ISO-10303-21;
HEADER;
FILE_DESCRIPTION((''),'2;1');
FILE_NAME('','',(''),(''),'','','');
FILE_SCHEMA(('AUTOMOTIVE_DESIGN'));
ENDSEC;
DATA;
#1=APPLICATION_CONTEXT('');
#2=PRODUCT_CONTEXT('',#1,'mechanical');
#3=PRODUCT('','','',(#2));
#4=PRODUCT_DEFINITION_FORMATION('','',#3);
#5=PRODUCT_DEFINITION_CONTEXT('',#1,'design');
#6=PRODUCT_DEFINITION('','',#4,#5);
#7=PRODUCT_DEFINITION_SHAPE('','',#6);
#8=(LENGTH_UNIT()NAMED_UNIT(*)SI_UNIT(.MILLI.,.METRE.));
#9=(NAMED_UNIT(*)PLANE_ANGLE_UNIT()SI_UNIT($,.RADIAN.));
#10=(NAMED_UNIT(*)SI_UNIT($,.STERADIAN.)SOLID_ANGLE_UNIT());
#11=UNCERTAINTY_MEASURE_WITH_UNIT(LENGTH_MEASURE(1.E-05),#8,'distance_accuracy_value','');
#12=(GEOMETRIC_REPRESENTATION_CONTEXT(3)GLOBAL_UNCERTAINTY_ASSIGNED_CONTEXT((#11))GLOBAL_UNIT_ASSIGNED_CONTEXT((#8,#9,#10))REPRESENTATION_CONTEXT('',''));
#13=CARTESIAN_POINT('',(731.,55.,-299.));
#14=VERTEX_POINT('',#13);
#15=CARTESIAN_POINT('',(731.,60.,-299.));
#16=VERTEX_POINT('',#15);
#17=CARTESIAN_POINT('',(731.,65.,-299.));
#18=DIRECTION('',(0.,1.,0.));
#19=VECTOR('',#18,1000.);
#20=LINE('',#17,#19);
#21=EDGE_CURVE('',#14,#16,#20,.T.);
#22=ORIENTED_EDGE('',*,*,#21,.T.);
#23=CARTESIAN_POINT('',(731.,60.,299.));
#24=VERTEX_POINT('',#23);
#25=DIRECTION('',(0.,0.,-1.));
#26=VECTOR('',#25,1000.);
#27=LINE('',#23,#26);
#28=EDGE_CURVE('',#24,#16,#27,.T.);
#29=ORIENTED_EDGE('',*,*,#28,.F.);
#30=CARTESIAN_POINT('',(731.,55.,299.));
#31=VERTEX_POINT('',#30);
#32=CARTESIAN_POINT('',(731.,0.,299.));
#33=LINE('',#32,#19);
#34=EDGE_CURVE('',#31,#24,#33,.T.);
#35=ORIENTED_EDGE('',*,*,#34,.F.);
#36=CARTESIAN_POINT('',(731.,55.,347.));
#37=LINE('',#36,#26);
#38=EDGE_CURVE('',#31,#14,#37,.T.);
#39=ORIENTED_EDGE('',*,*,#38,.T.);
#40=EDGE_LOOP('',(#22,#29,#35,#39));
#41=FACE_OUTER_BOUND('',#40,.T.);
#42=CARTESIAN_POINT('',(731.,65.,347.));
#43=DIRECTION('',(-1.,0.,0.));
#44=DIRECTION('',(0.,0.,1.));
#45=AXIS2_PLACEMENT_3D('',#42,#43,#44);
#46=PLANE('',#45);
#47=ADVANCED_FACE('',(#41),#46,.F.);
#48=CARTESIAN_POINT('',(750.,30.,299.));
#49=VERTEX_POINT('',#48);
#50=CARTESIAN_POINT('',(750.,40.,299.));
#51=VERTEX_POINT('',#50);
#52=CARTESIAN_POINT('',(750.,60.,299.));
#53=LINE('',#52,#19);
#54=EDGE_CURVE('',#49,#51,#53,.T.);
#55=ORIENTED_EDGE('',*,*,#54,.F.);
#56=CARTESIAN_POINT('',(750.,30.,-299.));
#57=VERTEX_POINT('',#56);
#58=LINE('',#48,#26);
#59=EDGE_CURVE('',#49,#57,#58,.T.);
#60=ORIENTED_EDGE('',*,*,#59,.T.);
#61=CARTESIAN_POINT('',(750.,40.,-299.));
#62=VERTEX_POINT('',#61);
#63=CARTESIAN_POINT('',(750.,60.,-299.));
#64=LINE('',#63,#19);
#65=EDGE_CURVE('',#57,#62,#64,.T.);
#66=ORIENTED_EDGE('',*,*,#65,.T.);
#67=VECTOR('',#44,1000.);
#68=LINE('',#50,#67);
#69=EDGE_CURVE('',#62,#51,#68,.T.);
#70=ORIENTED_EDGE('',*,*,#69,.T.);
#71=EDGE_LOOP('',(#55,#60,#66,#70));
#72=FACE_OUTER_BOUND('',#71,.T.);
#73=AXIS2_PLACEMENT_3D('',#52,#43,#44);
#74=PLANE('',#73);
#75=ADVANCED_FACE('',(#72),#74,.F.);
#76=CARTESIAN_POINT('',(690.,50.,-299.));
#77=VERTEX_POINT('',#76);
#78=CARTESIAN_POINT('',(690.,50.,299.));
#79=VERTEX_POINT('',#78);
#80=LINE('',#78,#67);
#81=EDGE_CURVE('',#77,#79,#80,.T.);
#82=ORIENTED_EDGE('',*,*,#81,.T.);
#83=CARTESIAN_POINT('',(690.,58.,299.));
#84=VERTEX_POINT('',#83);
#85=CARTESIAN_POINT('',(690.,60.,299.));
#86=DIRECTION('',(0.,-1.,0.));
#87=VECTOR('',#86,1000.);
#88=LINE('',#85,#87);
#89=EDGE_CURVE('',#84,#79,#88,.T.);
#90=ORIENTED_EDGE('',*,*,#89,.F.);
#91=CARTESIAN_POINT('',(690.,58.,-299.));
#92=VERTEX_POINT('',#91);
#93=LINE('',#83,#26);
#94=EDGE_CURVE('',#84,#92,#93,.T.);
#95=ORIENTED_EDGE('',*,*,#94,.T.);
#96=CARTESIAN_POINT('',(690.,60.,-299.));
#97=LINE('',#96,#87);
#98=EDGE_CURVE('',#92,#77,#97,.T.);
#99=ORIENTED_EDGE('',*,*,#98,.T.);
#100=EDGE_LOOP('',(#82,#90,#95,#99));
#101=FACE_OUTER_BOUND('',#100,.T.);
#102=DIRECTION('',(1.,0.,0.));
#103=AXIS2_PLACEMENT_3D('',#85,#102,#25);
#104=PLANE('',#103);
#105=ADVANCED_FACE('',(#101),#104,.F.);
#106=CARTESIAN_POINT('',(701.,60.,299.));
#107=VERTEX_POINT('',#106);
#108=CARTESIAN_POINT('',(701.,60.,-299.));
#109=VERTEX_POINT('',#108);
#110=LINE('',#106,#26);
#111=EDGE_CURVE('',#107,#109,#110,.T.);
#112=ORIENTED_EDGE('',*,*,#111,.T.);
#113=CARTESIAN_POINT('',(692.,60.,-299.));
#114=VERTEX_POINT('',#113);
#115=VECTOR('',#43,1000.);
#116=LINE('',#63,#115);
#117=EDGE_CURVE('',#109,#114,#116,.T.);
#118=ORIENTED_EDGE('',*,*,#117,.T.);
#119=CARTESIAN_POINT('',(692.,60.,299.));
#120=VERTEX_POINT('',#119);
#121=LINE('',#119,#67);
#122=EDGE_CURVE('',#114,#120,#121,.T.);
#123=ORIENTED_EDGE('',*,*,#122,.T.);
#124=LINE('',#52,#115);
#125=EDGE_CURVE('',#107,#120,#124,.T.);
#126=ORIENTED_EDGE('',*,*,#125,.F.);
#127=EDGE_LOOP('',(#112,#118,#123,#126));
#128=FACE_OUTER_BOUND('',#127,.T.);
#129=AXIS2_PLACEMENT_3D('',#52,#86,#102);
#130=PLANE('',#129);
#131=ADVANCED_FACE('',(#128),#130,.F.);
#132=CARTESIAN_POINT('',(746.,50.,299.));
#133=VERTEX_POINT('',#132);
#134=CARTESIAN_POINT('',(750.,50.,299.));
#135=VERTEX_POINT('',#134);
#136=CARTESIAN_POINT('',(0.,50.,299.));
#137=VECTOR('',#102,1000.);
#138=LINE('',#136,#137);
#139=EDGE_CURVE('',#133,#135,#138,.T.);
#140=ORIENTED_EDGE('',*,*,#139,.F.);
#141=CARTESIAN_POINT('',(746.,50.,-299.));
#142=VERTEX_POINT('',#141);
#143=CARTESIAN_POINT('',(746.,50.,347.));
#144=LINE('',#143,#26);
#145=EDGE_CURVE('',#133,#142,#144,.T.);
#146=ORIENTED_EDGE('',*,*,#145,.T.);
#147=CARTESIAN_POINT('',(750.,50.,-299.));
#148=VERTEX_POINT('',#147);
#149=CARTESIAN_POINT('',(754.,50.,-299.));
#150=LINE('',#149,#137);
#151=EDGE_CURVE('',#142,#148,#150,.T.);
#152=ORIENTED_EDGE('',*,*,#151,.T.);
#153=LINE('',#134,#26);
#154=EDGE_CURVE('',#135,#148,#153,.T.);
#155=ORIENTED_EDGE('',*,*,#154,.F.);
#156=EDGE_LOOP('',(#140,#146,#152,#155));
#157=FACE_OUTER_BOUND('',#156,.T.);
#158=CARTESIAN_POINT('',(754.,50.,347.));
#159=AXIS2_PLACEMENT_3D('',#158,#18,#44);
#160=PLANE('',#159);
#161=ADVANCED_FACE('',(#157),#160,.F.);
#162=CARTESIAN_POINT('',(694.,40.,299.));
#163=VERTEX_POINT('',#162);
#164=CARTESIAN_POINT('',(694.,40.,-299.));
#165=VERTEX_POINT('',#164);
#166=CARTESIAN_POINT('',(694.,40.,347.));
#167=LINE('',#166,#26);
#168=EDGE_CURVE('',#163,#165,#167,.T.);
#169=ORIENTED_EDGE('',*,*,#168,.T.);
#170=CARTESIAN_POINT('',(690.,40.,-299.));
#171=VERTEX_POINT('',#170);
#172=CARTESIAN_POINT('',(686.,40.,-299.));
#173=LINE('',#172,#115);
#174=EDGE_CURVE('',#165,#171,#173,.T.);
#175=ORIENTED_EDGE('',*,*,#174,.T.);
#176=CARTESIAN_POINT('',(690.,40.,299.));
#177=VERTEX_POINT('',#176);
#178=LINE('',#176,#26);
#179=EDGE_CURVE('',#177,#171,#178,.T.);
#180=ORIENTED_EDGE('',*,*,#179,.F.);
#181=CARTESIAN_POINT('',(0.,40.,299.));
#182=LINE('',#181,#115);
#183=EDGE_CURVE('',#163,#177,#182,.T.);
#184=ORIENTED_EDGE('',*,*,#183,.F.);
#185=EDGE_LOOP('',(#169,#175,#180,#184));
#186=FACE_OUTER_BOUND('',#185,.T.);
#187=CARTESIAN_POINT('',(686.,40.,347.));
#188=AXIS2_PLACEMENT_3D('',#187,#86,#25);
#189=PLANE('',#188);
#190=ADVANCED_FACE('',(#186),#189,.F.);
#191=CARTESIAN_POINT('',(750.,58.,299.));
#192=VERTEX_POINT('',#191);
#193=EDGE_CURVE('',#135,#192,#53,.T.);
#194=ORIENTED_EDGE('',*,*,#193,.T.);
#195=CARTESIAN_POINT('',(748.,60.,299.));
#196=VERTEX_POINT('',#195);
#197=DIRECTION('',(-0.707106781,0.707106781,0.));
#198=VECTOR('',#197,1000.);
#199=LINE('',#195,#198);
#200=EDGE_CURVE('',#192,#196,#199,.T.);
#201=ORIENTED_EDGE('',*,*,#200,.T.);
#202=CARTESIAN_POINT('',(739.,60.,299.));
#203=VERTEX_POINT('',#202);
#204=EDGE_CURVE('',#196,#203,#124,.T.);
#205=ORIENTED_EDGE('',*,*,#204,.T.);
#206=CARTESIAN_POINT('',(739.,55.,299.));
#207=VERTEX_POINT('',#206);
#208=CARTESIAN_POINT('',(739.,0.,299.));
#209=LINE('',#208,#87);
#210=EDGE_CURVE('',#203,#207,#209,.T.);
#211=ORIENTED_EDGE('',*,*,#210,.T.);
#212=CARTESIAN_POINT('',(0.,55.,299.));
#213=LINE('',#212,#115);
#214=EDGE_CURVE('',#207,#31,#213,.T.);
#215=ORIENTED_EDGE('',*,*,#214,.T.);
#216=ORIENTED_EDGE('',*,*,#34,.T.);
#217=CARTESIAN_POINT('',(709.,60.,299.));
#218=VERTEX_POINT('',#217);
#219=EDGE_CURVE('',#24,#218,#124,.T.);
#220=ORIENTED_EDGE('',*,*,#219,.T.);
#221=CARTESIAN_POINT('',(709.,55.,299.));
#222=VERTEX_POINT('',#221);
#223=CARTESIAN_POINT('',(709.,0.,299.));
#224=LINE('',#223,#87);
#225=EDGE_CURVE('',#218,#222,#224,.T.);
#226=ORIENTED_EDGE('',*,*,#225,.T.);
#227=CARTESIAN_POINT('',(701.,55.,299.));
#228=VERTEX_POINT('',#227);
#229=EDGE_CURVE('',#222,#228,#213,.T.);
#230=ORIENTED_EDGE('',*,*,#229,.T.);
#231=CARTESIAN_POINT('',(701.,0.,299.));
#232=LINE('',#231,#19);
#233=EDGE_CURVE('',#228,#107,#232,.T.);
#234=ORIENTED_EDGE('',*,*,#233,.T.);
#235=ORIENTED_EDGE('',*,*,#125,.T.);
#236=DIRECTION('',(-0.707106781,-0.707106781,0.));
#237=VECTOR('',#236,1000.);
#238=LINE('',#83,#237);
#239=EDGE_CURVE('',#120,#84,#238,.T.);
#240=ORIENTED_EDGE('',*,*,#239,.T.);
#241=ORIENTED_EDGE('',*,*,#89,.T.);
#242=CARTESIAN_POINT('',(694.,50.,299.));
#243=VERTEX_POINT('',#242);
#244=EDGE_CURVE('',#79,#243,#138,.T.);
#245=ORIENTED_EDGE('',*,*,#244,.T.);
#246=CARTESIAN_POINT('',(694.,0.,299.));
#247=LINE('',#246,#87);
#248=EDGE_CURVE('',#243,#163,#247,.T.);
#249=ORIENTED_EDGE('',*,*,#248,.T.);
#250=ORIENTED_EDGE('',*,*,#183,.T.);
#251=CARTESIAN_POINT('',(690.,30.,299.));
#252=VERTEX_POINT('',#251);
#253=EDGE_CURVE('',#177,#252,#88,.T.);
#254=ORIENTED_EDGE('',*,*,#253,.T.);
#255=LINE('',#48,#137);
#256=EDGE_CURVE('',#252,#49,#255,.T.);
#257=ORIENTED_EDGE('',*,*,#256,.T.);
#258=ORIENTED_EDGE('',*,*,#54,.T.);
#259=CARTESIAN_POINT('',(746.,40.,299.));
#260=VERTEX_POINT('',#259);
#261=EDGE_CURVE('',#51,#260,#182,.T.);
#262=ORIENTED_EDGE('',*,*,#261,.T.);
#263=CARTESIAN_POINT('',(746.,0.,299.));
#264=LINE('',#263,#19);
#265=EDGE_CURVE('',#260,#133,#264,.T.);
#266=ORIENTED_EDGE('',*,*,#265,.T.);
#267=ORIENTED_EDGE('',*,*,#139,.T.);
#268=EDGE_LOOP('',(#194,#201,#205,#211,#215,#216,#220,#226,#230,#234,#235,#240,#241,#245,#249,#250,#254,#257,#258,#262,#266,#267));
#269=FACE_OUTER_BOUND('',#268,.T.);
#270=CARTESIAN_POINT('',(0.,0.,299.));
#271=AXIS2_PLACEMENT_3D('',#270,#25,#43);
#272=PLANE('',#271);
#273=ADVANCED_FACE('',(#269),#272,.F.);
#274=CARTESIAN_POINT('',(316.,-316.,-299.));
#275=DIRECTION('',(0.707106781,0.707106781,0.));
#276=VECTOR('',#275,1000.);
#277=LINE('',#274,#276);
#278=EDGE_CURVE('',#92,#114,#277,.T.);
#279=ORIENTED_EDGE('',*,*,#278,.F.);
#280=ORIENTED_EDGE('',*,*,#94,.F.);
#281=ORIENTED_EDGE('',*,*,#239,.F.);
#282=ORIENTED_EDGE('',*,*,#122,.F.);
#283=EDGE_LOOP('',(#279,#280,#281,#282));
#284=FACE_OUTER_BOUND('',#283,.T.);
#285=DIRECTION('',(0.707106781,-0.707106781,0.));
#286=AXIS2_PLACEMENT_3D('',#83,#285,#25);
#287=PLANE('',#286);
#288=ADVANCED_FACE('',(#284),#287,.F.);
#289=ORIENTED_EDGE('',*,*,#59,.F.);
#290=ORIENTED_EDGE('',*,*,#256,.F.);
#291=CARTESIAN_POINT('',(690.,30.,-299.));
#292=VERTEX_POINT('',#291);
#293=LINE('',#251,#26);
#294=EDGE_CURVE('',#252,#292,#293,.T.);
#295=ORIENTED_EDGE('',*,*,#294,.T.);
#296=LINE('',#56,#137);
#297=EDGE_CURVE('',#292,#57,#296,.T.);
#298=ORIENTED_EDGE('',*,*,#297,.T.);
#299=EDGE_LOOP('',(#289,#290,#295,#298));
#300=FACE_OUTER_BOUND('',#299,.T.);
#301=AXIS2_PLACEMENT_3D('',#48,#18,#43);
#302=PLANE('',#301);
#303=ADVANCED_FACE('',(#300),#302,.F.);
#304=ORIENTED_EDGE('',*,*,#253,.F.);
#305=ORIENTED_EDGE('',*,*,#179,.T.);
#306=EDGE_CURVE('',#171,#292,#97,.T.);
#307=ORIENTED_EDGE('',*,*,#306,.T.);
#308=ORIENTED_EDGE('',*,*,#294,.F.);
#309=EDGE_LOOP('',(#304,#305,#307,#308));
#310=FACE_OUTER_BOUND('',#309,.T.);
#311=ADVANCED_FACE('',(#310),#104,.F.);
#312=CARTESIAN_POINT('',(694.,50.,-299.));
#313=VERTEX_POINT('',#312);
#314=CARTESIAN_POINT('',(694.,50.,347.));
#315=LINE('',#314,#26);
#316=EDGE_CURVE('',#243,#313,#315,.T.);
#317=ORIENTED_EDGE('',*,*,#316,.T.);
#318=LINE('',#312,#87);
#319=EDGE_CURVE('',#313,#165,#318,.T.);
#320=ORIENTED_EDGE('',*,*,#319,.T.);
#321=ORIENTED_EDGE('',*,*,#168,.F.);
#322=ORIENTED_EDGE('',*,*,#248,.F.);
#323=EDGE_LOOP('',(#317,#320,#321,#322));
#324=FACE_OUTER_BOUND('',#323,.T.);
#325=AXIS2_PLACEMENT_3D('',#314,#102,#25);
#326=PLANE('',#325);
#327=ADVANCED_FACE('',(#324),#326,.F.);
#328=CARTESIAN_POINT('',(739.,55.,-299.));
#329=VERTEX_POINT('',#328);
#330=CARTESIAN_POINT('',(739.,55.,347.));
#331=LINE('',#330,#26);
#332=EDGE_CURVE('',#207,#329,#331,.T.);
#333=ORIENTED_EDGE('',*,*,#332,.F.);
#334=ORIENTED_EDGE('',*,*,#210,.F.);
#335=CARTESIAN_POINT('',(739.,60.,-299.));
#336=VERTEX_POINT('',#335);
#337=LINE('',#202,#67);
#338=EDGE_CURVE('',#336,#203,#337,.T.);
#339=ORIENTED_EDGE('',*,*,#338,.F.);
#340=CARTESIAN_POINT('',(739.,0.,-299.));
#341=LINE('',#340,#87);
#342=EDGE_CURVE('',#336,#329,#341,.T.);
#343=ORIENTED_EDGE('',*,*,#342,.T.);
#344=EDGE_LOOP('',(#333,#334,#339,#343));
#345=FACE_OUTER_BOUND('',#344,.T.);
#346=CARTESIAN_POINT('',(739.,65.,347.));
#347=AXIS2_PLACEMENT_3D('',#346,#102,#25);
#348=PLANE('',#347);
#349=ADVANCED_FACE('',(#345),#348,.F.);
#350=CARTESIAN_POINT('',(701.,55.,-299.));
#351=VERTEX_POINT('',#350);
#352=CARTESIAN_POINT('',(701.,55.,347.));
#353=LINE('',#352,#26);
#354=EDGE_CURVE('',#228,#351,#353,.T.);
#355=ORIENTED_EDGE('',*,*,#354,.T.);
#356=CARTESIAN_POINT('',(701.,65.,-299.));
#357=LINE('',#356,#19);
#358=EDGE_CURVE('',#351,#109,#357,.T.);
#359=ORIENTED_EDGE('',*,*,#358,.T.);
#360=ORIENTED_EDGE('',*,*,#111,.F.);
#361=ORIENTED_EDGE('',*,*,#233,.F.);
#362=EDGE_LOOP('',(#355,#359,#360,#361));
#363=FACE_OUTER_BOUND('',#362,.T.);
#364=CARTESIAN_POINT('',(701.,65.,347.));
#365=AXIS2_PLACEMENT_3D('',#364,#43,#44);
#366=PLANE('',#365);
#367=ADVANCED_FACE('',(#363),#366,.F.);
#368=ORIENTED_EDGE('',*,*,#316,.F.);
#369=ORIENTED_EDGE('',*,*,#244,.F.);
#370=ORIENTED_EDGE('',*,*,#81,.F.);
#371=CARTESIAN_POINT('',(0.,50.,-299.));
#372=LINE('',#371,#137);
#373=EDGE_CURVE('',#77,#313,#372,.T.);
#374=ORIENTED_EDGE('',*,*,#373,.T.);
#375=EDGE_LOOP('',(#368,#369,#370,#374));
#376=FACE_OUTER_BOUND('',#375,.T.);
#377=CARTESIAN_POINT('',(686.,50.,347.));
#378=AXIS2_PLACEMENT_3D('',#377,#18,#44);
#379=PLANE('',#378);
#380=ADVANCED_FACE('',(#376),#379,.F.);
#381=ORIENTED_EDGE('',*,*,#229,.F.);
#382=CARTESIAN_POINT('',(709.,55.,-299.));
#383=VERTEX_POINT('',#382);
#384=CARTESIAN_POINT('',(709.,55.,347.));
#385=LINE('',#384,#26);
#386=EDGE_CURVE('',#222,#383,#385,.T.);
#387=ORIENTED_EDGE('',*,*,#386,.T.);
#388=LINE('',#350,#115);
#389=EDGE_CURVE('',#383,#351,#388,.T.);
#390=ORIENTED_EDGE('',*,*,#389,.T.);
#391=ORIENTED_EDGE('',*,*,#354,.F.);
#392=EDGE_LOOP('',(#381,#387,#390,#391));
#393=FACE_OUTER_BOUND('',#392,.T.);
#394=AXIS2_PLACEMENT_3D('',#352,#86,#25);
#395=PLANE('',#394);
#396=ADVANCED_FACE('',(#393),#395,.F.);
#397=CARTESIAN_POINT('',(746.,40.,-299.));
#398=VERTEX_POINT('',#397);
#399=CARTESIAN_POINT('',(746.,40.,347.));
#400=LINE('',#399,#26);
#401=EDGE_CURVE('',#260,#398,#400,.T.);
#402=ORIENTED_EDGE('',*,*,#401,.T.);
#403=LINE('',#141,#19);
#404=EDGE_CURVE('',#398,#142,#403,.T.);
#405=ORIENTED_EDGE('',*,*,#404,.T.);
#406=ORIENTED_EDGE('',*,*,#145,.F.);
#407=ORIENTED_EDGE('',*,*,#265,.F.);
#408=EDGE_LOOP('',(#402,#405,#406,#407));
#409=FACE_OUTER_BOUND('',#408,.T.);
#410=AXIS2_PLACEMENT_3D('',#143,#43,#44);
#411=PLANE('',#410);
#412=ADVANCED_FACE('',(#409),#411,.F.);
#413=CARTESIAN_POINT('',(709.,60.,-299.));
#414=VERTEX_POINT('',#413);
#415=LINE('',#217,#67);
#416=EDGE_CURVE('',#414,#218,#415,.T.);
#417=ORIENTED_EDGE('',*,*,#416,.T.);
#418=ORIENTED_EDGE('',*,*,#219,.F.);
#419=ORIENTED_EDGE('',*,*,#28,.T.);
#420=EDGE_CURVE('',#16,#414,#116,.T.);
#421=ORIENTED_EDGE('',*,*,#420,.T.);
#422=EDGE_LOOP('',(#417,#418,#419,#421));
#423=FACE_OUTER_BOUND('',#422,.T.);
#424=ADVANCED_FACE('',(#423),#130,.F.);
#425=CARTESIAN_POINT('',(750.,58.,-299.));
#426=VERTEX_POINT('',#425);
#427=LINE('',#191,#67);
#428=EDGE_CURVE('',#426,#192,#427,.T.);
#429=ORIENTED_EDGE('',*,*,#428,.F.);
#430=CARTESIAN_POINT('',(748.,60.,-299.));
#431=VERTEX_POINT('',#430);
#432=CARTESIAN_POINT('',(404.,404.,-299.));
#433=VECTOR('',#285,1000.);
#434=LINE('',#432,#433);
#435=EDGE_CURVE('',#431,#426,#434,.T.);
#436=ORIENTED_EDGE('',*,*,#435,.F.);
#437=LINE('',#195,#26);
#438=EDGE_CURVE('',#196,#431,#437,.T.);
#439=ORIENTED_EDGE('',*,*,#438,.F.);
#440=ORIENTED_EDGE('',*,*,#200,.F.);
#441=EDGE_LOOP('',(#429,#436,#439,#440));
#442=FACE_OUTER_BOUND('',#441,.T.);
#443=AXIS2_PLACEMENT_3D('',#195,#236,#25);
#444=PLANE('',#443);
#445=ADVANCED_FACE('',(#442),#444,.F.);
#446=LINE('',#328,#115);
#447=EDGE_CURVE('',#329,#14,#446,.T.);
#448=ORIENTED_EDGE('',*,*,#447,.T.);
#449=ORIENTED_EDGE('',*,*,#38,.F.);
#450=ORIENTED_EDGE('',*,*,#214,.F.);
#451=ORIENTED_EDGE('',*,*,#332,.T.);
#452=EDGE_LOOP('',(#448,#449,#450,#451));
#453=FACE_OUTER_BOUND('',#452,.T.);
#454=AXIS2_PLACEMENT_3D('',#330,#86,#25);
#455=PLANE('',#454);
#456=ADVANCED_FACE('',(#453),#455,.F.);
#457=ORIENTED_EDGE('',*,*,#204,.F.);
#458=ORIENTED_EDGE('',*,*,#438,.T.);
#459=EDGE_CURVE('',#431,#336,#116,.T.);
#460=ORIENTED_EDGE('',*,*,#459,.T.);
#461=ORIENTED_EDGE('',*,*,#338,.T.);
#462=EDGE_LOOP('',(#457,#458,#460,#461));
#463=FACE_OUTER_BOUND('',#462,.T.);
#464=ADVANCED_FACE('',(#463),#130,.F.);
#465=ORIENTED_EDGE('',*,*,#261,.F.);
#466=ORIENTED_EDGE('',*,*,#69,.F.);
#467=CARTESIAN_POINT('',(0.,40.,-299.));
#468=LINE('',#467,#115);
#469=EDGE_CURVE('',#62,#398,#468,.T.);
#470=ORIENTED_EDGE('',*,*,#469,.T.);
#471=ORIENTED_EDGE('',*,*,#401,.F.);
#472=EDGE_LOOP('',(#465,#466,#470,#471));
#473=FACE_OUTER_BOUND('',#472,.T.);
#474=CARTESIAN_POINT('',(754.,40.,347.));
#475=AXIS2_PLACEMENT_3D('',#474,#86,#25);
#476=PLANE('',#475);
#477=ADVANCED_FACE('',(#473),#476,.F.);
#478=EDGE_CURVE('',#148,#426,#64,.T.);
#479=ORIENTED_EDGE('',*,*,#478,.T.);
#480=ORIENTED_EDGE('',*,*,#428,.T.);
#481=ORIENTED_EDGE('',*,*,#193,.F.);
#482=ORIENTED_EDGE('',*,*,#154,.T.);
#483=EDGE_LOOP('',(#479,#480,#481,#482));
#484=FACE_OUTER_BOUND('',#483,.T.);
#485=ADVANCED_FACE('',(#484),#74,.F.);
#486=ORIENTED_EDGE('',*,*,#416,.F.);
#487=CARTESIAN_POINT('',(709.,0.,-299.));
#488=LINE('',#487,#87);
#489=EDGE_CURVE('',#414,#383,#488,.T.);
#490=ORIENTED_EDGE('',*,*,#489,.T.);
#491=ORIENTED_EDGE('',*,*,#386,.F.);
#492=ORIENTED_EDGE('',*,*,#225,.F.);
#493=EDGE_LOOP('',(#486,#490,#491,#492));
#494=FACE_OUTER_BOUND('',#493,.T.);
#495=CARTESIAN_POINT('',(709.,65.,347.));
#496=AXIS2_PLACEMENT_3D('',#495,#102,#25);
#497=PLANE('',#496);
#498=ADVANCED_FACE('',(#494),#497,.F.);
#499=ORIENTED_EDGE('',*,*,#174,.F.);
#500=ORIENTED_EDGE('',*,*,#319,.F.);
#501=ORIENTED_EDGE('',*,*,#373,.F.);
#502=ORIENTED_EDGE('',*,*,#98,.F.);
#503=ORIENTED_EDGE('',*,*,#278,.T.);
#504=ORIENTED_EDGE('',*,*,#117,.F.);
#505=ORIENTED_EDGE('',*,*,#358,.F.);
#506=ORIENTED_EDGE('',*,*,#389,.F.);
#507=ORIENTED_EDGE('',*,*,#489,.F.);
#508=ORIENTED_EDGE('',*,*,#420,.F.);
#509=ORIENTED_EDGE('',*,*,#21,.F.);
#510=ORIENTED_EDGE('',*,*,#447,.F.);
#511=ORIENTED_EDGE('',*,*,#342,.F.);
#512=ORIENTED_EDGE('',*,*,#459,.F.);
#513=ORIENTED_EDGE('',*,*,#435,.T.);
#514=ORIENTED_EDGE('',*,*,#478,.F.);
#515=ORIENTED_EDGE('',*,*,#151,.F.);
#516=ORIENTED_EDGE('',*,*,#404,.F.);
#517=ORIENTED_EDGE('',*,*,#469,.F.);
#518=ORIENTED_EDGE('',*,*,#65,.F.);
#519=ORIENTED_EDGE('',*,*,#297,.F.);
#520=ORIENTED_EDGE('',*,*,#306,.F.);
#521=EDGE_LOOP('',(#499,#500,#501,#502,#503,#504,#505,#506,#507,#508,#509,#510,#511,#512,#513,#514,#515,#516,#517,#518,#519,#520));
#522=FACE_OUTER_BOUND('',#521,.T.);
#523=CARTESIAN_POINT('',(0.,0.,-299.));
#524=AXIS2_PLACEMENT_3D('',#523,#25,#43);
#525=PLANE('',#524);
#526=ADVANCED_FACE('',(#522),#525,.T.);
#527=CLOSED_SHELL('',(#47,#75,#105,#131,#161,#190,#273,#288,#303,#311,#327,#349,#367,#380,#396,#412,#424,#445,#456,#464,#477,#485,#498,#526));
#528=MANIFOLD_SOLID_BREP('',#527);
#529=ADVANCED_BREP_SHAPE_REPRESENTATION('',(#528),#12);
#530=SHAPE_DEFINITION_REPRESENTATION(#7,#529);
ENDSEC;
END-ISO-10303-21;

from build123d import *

# Parameters (mm, degrees)
SKETCH1_W           = 60
SKETCH1_H           = 30
BOSS_EXTRUDE1_DEPTH = 299
SKETCH2_W           = 8
SKETCH2_H           = 10
CUT_EXTRUDE1_DEPTH  = 646
CHAMFER1_SIZE       = 2


with BuildPart() as part:
    # Sketch1 → Boss-Extrude1 (new, symmetric)
    with BuildSketch(Plane.XY):
        with Locations((720, 45)):
            Rectangle(SKETCH1_W, SKETCH1_H)
    extrude(amount=BOSS_EXTRUDE1_DEPTH, both=True)

    # Sketch2 → Cut-Extrude1 (cut)
    with BuildSketch(Plane(origin=(0, 0, -299), x_dir=(-1, 0, 0), z_dir=(0, 0, -1))):
        with Locations((-735, 60)):
            Rectangle(SKETCH2_W, SKETCH2_H)
        with Locations((-750, 45)):
            Rectangle(SKETCH2_W, SKETCH2_H)
        with Locations((-690, 45)):
            Rectangle(SKETCH2_W, SKETCH2_H)
        with Locations((-705, 60)):
            Rectangle(SKETCH2_W, SKETCH2_H)
    extrude(amount=-CUT_EXTRUDE1_DEPTH, mode=Mode.SUBTRACT)

    # Chamfer1
    chamfer1_edges = [part.edges().sort_by_distance(p)[0] for p in [
        (690, 60, 0),
        (750, 60, 0),
    ]]
    chamfer(chamfer1_edges, length=CHAMFER1_SIZE)


solid = part.part
